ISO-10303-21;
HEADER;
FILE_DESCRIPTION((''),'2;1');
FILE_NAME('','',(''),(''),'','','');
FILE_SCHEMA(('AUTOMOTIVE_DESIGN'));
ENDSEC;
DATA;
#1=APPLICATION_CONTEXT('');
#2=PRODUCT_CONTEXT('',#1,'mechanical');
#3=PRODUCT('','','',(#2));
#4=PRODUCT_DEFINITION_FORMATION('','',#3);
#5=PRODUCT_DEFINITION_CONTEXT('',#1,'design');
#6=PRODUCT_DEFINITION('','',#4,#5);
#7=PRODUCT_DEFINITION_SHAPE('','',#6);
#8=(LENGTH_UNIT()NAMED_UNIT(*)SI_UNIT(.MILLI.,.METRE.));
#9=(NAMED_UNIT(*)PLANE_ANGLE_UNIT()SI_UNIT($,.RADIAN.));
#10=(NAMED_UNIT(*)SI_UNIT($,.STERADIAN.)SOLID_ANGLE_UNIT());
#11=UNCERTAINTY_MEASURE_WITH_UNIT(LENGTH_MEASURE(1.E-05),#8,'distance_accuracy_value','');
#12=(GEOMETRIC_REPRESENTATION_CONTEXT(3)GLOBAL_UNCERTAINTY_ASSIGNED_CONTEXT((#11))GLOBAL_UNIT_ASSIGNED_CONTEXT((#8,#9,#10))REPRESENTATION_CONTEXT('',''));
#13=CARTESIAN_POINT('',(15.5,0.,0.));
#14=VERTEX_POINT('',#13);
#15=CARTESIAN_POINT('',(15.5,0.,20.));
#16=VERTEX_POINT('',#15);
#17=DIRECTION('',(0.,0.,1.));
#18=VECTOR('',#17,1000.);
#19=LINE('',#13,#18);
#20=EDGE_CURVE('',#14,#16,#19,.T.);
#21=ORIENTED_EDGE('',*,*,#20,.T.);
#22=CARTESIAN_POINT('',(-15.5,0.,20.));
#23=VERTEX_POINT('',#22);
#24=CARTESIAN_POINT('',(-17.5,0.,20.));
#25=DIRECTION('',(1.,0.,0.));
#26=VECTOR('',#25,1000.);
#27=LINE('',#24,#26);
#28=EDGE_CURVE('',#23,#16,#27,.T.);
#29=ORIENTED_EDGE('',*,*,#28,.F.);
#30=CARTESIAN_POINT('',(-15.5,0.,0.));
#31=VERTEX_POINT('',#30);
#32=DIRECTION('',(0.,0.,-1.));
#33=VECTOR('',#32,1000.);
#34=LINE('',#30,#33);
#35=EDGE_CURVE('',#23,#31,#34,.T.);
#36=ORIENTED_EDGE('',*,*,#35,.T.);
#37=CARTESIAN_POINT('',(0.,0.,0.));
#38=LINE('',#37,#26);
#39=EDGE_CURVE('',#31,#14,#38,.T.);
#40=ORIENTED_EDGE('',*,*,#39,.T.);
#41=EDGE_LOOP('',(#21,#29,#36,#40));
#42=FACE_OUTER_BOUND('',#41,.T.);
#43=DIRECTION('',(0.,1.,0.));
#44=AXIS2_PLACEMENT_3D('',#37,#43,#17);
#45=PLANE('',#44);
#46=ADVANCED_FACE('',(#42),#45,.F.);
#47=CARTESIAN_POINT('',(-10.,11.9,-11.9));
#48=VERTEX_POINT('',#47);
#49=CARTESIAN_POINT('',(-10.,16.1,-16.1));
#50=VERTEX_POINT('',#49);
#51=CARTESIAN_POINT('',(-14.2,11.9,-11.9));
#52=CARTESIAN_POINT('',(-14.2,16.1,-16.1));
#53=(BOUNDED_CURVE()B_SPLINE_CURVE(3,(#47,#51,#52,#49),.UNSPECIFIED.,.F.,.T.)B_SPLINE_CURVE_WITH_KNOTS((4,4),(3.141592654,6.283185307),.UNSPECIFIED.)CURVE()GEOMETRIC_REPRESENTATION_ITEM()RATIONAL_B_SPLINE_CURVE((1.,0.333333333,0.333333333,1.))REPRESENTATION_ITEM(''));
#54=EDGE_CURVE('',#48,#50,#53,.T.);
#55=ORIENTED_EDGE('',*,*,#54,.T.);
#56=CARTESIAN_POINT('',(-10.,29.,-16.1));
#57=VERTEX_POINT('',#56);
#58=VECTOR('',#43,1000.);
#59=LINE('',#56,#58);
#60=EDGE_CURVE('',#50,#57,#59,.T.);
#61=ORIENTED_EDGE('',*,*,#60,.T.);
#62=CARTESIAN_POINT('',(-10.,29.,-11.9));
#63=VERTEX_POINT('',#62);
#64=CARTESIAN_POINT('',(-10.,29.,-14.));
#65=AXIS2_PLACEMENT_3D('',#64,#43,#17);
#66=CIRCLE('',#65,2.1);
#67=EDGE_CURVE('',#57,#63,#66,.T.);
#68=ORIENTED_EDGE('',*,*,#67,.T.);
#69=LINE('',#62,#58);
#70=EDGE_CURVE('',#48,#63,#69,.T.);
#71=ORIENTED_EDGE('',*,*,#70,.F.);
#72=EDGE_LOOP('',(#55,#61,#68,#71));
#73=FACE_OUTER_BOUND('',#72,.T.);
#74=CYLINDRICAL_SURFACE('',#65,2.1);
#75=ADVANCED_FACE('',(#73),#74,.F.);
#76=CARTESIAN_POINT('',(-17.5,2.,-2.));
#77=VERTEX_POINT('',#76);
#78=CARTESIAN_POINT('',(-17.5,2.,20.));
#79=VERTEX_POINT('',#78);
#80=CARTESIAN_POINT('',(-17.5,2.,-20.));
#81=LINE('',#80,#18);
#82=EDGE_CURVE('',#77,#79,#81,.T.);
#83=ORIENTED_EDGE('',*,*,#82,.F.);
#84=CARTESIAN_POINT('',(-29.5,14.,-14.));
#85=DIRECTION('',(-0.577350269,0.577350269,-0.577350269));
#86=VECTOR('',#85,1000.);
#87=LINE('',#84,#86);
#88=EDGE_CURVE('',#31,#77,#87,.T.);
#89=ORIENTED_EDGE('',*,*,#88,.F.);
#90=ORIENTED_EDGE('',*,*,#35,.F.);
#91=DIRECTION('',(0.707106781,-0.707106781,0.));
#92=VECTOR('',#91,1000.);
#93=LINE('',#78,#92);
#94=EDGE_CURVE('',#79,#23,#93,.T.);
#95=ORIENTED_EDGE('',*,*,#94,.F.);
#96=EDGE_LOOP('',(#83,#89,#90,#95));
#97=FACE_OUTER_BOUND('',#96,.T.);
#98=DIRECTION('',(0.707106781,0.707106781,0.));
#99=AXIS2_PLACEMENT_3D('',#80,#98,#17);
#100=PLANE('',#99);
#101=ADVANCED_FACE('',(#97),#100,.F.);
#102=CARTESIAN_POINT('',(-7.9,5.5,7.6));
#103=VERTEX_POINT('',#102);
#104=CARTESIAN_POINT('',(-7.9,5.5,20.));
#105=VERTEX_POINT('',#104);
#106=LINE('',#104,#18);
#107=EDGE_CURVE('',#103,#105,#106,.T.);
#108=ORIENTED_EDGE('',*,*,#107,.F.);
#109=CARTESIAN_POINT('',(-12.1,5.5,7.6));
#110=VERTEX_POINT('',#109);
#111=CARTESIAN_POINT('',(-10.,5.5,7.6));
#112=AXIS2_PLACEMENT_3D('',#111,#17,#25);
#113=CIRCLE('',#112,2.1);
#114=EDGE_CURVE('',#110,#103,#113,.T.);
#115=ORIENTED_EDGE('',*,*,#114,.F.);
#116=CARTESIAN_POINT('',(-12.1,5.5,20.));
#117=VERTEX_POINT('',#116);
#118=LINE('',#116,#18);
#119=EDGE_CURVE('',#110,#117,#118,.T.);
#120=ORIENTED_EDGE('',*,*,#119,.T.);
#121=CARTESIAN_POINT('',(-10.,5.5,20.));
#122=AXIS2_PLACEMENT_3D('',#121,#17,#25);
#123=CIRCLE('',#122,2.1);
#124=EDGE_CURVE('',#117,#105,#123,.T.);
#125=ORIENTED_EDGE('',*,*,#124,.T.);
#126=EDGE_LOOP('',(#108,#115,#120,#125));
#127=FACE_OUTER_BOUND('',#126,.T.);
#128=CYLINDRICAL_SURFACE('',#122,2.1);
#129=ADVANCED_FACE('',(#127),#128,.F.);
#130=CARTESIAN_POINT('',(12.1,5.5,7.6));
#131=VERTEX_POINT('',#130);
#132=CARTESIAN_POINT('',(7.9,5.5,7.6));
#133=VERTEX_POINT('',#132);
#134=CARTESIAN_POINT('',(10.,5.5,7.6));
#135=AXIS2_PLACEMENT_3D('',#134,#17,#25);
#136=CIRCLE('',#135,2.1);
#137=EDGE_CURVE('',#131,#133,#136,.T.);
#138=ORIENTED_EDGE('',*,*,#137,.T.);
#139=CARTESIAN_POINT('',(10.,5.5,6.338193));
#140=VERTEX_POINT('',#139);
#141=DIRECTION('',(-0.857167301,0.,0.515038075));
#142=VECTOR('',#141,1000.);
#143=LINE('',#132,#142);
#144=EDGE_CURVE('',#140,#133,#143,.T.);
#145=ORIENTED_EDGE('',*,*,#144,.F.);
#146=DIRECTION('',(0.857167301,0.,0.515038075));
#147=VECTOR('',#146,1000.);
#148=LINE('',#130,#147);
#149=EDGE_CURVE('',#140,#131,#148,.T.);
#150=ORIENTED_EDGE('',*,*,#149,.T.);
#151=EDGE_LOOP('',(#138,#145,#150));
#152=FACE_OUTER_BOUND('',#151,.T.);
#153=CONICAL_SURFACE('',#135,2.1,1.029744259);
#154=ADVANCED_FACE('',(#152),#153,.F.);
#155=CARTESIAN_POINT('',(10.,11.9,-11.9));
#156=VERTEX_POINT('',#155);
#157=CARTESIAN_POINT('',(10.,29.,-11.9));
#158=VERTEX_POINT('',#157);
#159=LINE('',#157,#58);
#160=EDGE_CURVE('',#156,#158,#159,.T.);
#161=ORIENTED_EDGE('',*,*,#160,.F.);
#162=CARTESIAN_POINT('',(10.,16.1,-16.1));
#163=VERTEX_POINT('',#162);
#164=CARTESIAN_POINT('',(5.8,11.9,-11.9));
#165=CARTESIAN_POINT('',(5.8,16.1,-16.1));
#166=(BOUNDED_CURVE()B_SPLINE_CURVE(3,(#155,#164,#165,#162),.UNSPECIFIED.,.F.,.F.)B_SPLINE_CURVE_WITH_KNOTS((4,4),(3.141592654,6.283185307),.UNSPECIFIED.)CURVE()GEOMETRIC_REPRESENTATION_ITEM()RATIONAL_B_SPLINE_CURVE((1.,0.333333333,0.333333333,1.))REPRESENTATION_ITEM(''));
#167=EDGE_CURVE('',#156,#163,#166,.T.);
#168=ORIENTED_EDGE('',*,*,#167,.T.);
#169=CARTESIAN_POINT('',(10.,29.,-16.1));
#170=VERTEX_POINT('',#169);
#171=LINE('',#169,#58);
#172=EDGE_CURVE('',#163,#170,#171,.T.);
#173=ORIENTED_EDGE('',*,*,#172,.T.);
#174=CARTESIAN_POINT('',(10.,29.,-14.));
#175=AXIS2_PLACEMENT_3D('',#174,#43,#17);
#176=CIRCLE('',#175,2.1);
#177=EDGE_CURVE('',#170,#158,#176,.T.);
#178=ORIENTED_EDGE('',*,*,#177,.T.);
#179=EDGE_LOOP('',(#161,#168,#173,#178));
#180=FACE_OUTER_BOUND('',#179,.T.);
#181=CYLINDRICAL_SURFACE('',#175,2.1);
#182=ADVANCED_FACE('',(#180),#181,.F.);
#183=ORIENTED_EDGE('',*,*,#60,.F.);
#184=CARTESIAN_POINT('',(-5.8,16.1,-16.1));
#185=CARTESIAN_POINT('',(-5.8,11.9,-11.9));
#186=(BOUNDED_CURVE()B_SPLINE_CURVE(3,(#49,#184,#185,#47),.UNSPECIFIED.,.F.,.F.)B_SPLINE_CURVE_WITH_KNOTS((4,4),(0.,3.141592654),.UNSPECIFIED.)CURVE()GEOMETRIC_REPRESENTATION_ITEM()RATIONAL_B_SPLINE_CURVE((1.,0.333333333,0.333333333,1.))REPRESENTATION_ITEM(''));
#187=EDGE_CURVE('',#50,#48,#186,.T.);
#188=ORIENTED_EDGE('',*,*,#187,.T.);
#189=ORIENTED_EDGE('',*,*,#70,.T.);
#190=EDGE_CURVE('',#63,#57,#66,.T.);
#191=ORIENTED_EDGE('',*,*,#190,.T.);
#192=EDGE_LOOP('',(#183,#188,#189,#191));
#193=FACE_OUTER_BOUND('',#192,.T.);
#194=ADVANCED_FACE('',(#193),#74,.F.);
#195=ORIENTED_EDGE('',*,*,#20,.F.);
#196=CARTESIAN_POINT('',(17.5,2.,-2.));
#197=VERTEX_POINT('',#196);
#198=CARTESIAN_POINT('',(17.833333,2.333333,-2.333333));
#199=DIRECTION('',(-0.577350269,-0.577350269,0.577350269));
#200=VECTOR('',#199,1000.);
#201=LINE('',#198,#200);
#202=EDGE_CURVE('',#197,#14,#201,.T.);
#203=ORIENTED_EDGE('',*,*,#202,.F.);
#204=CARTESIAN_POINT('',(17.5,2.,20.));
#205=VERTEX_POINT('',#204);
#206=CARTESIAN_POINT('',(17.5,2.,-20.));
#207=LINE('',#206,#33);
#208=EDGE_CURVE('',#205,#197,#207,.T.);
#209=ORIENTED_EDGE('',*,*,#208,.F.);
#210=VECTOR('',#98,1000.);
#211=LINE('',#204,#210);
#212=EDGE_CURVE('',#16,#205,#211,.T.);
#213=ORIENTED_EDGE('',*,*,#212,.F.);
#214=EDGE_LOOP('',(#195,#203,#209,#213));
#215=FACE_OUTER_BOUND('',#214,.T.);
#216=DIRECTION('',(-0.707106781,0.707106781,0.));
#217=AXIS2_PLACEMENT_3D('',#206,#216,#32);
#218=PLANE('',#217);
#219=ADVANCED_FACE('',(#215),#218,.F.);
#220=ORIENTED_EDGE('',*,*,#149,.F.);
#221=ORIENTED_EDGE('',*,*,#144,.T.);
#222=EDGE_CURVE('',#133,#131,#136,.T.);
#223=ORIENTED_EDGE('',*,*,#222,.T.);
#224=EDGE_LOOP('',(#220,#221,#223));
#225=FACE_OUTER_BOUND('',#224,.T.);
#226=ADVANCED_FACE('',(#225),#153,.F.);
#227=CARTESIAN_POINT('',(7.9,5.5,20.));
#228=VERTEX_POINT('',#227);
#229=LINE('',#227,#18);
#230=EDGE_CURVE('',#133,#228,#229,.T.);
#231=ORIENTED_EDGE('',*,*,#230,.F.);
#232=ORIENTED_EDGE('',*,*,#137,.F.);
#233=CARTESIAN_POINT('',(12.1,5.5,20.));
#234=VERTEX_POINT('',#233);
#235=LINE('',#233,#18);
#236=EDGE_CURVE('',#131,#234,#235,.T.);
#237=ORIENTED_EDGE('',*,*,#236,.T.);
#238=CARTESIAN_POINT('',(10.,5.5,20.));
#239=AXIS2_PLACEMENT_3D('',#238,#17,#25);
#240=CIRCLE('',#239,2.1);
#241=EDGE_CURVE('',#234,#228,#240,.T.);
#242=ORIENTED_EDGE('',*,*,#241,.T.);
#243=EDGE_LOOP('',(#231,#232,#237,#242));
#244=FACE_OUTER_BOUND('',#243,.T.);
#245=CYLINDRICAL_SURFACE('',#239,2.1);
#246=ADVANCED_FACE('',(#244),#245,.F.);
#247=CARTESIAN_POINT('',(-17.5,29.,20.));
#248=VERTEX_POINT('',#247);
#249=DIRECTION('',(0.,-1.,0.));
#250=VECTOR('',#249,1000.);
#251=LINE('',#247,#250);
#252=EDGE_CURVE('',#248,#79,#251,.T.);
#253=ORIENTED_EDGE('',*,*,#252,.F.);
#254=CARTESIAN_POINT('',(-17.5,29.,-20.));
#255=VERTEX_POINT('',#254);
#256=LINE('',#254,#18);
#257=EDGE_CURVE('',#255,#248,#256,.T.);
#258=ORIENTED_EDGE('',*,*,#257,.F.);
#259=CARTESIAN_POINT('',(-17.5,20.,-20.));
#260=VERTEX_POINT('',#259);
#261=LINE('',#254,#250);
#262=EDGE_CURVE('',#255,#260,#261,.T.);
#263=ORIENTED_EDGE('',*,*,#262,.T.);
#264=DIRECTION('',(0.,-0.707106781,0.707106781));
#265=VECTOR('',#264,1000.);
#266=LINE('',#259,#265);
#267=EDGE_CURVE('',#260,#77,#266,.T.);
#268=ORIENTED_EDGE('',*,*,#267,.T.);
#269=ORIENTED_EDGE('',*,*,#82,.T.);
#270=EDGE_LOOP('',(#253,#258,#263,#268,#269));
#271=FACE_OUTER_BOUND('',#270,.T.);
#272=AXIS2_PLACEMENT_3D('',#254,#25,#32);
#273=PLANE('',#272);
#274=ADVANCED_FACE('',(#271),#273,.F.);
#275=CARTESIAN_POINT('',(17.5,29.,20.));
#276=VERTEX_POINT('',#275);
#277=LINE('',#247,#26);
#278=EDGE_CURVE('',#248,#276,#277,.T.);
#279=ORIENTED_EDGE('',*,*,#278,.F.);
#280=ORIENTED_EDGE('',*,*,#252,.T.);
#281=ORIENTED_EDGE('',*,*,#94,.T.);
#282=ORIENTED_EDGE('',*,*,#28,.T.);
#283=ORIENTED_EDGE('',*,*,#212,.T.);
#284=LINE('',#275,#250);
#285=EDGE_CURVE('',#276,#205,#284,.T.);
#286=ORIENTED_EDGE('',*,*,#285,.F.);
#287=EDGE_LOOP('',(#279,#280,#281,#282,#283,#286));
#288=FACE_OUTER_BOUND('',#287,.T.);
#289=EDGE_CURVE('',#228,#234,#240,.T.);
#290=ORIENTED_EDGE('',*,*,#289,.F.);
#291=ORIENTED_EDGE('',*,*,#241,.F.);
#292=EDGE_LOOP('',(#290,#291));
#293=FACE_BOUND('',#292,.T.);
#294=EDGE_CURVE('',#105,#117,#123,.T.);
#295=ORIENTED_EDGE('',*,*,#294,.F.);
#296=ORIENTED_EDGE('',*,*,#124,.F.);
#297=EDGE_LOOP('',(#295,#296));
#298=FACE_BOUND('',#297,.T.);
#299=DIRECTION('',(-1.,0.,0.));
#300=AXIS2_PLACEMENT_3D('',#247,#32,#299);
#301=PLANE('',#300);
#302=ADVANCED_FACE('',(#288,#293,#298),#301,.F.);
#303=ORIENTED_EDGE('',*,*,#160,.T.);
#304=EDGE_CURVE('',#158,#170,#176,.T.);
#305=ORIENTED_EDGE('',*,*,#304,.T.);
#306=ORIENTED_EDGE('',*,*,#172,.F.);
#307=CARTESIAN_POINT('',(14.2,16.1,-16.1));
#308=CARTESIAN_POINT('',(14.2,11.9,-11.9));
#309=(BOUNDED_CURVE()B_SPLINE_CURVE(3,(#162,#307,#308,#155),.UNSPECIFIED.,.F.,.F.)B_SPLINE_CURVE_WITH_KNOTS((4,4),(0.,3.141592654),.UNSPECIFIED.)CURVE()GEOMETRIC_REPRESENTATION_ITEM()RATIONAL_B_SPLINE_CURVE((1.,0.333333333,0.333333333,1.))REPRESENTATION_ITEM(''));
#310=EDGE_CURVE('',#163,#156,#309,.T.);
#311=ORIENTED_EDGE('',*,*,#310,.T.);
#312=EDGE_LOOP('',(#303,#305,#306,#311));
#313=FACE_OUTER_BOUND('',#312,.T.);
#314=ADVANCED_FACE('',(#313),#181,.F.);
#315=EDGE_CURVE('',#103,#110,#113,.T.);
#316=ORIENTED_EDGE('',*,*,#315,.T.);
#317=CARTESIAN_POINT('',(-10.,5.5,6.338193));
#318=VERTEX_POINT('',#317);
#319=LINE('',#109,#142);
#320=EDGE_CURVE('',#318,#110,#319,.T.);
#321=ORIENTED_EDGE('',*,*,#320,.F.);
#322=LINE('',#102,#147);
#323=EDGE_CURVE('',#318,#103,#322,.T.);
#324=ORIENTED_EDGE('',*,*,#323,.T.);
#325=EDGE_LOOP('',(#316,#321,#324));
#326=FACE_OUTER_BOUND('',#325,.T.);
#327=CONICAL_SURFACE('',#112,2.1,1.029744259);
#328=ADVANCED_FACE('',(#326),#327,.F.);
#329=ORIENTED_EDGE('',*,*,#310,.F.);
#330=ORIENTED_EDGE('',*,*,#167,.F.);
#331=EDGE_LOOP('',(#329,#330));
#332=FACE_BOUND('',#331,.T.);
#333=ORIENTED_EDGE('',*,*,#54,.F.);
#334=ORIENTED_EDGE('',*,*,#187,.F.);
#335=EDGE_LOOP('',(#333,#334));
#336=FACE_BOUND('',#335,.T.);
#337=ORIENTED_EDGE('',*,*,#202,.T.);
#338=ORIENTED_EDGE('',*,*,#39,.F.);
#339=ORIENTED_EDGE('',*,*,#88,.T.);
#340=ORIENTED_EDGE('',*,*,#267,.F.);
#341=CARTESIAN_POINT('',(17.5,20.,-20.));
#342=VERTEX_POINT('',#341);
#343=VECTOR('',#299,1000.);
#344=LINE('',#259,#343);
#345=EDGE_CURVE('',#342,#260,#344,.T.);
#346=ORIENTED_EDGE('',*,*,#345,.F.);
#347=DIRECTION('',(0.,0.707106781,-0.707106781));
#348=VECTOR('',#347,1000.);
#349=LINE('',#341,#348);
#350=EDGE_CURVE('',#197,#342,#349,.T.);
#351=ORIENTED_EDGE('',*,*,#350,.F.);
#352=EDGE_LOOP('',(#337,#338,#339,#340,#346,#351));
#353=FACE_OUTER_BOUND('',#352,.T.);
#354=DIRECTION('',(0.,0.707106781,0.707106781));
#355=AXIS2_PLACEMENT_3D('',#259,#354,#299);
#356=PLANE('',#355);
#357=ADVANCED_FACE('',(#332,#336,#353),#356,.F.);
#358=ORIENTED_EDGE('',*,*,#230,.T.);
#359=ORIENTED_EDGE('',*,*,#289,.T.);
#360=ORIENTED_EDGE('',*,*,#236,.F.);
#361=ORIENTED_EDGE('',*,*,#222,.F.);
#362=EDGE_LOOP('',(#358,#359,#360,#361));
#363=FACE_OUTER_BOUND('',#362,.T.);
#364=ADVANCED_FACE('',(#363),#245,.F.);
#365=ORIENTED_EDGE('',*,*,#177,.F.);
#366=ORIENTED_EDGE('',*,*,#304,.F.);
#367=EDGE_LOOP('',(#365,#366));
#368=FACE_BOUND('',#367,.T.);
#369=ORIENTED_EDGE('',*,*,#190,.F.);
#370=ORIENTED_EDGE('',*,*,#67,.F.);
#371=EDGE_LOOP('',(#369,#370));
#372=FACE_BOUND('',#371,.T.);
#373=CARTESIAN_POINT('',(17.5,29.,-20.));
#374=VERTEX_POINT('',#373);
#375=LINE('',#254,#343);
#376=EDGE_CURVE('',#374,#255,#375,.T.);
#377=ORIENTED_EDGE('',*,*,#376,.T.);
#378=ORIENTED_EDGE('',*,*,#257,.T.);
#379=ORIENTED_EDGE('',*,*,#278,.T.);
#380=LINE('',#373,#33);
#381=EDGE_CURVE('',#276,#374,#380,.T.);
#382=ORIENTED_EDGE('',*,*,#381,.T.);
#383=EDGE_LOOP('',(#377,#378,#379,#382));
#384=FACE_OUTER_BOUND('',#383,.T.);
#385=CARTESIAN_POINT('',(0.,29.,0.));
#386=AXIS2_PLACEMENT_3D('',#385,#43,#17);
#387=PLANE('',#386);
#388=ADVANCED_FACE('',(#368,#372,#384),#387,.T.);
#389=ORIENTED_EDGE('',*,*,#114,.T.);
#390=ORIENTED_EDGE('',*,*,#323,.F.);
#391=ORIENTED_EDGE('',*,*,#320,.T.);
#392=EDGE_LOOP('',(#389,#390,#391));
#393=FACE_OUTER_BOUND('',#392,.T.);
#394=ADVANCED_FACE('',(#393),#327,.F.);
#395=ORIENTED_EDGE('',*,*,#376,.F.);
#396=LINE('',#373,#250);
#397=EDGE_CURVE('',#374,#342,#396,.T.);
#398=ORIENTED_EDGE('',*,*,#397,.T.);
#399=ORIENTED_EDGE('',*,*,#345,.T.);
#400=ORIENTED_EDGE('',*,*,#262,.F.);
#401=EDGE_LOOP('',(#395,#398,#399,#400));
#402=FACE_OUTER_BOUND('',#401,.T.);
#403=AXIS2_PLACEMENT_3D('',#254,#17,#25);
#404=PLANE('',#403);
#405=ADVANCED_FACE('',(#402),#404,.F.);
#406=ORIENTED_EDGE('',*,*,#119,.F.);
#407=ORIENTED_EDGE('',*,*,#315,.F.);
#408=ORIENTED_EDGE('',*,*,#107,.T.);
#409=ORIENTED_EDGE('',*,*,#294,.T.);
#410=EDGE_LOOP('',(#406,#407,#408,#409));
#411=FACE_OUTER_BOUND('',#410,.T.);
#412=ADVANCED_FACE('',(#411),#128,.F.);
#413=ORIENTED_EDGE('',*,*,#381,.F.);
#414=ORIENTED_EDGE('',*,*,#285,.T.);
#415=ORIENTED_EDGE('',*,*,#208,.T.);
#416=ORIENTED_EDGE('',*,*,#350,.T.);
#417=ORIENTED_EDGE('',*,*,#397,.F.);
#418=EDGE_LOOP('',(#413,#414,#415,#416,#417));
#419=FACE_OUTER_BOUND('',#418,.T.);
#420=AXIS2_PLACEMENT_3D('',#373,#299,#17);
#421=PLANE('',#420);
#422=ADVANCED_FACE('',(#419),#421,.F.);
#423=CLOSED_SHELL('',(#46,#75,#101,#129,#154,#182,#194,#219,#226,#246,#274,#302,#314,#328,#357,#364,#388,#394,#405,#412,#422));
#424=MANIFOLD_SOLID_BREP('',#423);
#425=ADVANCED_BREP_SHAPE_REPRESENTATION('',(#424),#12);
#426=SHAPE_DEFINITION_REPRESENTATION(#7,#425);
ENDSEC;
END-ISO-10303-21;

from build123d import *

# Parameters (mm, degrees)
SKETCH1_W             = 35
SKETCH1_H             = 40
BOSS_EXTRUDE1_DEPTH   = 29
CHAMFER1_SIZE         = 20
M5_TAPPED_HOLE1_D     = 4.2
M5_TAPPED_HOLE1_DEPTH = 12.4
M5_TAPPED_HOLE1_TIP   = 1.2618073
M5_TAPPED_HOLE2_D     = 4.2
CHAMFER2_SIZE         = 2


with BuildPart() as part:
    # Sketch1 → Boss-Extrude1 (new body)
    with BuildSketch(Plane(origin=(0, 0, 0), x_dir=(1, 0, 0), z_dir=(0, 1, 0))):
        Rectangle(SKETCH1_W, SKETCH1_H)
    extrude(amount=BOSS_EXTRUDE1_DEPTH)

    # Chamfer1
    chamfer1_edges = [part.edges().sort_by_distance(p)[0] for p in [
        (0, 0, -20),
    ]]
    chamfer(chamfer1_edges, length=CHAMFER1_SIZE)

    # M5 Tapped Hole1
    with Locations(Plane(origin=(-10, 5.5, 20), x_dir=(1, 0, 0), z_dir=(0, 0, 1))):
        with Locations((0, 0), (20, 0)):
            Hole(M5_TAPPED_HOLE1_D / 2, depth=M5_TAPPED_HOLE1_DEPTH)
            with Locations((0, 0, -(M5_TAPPED_HOLE1_DEPTH + M5_TAPPED_HOLE1_TIP / 2))):  # 118° drill point
                Cone(0, M5_TAPPED_HOLE1_D / 2, M5_TAPPED_HOLE1_TIP, mode=Mode.SUBTRACT)

    # M5 Tapped Hole2 (through all)
    with Locations(Plane(origin=(-10, 29, -14), x_dir=(0, 0, 1), z_dir=(0, 1, 0))):
        with Locations((0, 0), (0, 20)):
            Hole(M5_TAPPED_HOLE2_D / 2)

    # Chamfer2
    chamfer2_edges = [part.edges().sort_by_distance(p)[0] for p in [
        (-17.5, 0, 10),
        (17.5, 0, 10),
    ]]
    chamfer(chamfer2_edges, length=CHAMFER2_SIZE)


solid = part.part
